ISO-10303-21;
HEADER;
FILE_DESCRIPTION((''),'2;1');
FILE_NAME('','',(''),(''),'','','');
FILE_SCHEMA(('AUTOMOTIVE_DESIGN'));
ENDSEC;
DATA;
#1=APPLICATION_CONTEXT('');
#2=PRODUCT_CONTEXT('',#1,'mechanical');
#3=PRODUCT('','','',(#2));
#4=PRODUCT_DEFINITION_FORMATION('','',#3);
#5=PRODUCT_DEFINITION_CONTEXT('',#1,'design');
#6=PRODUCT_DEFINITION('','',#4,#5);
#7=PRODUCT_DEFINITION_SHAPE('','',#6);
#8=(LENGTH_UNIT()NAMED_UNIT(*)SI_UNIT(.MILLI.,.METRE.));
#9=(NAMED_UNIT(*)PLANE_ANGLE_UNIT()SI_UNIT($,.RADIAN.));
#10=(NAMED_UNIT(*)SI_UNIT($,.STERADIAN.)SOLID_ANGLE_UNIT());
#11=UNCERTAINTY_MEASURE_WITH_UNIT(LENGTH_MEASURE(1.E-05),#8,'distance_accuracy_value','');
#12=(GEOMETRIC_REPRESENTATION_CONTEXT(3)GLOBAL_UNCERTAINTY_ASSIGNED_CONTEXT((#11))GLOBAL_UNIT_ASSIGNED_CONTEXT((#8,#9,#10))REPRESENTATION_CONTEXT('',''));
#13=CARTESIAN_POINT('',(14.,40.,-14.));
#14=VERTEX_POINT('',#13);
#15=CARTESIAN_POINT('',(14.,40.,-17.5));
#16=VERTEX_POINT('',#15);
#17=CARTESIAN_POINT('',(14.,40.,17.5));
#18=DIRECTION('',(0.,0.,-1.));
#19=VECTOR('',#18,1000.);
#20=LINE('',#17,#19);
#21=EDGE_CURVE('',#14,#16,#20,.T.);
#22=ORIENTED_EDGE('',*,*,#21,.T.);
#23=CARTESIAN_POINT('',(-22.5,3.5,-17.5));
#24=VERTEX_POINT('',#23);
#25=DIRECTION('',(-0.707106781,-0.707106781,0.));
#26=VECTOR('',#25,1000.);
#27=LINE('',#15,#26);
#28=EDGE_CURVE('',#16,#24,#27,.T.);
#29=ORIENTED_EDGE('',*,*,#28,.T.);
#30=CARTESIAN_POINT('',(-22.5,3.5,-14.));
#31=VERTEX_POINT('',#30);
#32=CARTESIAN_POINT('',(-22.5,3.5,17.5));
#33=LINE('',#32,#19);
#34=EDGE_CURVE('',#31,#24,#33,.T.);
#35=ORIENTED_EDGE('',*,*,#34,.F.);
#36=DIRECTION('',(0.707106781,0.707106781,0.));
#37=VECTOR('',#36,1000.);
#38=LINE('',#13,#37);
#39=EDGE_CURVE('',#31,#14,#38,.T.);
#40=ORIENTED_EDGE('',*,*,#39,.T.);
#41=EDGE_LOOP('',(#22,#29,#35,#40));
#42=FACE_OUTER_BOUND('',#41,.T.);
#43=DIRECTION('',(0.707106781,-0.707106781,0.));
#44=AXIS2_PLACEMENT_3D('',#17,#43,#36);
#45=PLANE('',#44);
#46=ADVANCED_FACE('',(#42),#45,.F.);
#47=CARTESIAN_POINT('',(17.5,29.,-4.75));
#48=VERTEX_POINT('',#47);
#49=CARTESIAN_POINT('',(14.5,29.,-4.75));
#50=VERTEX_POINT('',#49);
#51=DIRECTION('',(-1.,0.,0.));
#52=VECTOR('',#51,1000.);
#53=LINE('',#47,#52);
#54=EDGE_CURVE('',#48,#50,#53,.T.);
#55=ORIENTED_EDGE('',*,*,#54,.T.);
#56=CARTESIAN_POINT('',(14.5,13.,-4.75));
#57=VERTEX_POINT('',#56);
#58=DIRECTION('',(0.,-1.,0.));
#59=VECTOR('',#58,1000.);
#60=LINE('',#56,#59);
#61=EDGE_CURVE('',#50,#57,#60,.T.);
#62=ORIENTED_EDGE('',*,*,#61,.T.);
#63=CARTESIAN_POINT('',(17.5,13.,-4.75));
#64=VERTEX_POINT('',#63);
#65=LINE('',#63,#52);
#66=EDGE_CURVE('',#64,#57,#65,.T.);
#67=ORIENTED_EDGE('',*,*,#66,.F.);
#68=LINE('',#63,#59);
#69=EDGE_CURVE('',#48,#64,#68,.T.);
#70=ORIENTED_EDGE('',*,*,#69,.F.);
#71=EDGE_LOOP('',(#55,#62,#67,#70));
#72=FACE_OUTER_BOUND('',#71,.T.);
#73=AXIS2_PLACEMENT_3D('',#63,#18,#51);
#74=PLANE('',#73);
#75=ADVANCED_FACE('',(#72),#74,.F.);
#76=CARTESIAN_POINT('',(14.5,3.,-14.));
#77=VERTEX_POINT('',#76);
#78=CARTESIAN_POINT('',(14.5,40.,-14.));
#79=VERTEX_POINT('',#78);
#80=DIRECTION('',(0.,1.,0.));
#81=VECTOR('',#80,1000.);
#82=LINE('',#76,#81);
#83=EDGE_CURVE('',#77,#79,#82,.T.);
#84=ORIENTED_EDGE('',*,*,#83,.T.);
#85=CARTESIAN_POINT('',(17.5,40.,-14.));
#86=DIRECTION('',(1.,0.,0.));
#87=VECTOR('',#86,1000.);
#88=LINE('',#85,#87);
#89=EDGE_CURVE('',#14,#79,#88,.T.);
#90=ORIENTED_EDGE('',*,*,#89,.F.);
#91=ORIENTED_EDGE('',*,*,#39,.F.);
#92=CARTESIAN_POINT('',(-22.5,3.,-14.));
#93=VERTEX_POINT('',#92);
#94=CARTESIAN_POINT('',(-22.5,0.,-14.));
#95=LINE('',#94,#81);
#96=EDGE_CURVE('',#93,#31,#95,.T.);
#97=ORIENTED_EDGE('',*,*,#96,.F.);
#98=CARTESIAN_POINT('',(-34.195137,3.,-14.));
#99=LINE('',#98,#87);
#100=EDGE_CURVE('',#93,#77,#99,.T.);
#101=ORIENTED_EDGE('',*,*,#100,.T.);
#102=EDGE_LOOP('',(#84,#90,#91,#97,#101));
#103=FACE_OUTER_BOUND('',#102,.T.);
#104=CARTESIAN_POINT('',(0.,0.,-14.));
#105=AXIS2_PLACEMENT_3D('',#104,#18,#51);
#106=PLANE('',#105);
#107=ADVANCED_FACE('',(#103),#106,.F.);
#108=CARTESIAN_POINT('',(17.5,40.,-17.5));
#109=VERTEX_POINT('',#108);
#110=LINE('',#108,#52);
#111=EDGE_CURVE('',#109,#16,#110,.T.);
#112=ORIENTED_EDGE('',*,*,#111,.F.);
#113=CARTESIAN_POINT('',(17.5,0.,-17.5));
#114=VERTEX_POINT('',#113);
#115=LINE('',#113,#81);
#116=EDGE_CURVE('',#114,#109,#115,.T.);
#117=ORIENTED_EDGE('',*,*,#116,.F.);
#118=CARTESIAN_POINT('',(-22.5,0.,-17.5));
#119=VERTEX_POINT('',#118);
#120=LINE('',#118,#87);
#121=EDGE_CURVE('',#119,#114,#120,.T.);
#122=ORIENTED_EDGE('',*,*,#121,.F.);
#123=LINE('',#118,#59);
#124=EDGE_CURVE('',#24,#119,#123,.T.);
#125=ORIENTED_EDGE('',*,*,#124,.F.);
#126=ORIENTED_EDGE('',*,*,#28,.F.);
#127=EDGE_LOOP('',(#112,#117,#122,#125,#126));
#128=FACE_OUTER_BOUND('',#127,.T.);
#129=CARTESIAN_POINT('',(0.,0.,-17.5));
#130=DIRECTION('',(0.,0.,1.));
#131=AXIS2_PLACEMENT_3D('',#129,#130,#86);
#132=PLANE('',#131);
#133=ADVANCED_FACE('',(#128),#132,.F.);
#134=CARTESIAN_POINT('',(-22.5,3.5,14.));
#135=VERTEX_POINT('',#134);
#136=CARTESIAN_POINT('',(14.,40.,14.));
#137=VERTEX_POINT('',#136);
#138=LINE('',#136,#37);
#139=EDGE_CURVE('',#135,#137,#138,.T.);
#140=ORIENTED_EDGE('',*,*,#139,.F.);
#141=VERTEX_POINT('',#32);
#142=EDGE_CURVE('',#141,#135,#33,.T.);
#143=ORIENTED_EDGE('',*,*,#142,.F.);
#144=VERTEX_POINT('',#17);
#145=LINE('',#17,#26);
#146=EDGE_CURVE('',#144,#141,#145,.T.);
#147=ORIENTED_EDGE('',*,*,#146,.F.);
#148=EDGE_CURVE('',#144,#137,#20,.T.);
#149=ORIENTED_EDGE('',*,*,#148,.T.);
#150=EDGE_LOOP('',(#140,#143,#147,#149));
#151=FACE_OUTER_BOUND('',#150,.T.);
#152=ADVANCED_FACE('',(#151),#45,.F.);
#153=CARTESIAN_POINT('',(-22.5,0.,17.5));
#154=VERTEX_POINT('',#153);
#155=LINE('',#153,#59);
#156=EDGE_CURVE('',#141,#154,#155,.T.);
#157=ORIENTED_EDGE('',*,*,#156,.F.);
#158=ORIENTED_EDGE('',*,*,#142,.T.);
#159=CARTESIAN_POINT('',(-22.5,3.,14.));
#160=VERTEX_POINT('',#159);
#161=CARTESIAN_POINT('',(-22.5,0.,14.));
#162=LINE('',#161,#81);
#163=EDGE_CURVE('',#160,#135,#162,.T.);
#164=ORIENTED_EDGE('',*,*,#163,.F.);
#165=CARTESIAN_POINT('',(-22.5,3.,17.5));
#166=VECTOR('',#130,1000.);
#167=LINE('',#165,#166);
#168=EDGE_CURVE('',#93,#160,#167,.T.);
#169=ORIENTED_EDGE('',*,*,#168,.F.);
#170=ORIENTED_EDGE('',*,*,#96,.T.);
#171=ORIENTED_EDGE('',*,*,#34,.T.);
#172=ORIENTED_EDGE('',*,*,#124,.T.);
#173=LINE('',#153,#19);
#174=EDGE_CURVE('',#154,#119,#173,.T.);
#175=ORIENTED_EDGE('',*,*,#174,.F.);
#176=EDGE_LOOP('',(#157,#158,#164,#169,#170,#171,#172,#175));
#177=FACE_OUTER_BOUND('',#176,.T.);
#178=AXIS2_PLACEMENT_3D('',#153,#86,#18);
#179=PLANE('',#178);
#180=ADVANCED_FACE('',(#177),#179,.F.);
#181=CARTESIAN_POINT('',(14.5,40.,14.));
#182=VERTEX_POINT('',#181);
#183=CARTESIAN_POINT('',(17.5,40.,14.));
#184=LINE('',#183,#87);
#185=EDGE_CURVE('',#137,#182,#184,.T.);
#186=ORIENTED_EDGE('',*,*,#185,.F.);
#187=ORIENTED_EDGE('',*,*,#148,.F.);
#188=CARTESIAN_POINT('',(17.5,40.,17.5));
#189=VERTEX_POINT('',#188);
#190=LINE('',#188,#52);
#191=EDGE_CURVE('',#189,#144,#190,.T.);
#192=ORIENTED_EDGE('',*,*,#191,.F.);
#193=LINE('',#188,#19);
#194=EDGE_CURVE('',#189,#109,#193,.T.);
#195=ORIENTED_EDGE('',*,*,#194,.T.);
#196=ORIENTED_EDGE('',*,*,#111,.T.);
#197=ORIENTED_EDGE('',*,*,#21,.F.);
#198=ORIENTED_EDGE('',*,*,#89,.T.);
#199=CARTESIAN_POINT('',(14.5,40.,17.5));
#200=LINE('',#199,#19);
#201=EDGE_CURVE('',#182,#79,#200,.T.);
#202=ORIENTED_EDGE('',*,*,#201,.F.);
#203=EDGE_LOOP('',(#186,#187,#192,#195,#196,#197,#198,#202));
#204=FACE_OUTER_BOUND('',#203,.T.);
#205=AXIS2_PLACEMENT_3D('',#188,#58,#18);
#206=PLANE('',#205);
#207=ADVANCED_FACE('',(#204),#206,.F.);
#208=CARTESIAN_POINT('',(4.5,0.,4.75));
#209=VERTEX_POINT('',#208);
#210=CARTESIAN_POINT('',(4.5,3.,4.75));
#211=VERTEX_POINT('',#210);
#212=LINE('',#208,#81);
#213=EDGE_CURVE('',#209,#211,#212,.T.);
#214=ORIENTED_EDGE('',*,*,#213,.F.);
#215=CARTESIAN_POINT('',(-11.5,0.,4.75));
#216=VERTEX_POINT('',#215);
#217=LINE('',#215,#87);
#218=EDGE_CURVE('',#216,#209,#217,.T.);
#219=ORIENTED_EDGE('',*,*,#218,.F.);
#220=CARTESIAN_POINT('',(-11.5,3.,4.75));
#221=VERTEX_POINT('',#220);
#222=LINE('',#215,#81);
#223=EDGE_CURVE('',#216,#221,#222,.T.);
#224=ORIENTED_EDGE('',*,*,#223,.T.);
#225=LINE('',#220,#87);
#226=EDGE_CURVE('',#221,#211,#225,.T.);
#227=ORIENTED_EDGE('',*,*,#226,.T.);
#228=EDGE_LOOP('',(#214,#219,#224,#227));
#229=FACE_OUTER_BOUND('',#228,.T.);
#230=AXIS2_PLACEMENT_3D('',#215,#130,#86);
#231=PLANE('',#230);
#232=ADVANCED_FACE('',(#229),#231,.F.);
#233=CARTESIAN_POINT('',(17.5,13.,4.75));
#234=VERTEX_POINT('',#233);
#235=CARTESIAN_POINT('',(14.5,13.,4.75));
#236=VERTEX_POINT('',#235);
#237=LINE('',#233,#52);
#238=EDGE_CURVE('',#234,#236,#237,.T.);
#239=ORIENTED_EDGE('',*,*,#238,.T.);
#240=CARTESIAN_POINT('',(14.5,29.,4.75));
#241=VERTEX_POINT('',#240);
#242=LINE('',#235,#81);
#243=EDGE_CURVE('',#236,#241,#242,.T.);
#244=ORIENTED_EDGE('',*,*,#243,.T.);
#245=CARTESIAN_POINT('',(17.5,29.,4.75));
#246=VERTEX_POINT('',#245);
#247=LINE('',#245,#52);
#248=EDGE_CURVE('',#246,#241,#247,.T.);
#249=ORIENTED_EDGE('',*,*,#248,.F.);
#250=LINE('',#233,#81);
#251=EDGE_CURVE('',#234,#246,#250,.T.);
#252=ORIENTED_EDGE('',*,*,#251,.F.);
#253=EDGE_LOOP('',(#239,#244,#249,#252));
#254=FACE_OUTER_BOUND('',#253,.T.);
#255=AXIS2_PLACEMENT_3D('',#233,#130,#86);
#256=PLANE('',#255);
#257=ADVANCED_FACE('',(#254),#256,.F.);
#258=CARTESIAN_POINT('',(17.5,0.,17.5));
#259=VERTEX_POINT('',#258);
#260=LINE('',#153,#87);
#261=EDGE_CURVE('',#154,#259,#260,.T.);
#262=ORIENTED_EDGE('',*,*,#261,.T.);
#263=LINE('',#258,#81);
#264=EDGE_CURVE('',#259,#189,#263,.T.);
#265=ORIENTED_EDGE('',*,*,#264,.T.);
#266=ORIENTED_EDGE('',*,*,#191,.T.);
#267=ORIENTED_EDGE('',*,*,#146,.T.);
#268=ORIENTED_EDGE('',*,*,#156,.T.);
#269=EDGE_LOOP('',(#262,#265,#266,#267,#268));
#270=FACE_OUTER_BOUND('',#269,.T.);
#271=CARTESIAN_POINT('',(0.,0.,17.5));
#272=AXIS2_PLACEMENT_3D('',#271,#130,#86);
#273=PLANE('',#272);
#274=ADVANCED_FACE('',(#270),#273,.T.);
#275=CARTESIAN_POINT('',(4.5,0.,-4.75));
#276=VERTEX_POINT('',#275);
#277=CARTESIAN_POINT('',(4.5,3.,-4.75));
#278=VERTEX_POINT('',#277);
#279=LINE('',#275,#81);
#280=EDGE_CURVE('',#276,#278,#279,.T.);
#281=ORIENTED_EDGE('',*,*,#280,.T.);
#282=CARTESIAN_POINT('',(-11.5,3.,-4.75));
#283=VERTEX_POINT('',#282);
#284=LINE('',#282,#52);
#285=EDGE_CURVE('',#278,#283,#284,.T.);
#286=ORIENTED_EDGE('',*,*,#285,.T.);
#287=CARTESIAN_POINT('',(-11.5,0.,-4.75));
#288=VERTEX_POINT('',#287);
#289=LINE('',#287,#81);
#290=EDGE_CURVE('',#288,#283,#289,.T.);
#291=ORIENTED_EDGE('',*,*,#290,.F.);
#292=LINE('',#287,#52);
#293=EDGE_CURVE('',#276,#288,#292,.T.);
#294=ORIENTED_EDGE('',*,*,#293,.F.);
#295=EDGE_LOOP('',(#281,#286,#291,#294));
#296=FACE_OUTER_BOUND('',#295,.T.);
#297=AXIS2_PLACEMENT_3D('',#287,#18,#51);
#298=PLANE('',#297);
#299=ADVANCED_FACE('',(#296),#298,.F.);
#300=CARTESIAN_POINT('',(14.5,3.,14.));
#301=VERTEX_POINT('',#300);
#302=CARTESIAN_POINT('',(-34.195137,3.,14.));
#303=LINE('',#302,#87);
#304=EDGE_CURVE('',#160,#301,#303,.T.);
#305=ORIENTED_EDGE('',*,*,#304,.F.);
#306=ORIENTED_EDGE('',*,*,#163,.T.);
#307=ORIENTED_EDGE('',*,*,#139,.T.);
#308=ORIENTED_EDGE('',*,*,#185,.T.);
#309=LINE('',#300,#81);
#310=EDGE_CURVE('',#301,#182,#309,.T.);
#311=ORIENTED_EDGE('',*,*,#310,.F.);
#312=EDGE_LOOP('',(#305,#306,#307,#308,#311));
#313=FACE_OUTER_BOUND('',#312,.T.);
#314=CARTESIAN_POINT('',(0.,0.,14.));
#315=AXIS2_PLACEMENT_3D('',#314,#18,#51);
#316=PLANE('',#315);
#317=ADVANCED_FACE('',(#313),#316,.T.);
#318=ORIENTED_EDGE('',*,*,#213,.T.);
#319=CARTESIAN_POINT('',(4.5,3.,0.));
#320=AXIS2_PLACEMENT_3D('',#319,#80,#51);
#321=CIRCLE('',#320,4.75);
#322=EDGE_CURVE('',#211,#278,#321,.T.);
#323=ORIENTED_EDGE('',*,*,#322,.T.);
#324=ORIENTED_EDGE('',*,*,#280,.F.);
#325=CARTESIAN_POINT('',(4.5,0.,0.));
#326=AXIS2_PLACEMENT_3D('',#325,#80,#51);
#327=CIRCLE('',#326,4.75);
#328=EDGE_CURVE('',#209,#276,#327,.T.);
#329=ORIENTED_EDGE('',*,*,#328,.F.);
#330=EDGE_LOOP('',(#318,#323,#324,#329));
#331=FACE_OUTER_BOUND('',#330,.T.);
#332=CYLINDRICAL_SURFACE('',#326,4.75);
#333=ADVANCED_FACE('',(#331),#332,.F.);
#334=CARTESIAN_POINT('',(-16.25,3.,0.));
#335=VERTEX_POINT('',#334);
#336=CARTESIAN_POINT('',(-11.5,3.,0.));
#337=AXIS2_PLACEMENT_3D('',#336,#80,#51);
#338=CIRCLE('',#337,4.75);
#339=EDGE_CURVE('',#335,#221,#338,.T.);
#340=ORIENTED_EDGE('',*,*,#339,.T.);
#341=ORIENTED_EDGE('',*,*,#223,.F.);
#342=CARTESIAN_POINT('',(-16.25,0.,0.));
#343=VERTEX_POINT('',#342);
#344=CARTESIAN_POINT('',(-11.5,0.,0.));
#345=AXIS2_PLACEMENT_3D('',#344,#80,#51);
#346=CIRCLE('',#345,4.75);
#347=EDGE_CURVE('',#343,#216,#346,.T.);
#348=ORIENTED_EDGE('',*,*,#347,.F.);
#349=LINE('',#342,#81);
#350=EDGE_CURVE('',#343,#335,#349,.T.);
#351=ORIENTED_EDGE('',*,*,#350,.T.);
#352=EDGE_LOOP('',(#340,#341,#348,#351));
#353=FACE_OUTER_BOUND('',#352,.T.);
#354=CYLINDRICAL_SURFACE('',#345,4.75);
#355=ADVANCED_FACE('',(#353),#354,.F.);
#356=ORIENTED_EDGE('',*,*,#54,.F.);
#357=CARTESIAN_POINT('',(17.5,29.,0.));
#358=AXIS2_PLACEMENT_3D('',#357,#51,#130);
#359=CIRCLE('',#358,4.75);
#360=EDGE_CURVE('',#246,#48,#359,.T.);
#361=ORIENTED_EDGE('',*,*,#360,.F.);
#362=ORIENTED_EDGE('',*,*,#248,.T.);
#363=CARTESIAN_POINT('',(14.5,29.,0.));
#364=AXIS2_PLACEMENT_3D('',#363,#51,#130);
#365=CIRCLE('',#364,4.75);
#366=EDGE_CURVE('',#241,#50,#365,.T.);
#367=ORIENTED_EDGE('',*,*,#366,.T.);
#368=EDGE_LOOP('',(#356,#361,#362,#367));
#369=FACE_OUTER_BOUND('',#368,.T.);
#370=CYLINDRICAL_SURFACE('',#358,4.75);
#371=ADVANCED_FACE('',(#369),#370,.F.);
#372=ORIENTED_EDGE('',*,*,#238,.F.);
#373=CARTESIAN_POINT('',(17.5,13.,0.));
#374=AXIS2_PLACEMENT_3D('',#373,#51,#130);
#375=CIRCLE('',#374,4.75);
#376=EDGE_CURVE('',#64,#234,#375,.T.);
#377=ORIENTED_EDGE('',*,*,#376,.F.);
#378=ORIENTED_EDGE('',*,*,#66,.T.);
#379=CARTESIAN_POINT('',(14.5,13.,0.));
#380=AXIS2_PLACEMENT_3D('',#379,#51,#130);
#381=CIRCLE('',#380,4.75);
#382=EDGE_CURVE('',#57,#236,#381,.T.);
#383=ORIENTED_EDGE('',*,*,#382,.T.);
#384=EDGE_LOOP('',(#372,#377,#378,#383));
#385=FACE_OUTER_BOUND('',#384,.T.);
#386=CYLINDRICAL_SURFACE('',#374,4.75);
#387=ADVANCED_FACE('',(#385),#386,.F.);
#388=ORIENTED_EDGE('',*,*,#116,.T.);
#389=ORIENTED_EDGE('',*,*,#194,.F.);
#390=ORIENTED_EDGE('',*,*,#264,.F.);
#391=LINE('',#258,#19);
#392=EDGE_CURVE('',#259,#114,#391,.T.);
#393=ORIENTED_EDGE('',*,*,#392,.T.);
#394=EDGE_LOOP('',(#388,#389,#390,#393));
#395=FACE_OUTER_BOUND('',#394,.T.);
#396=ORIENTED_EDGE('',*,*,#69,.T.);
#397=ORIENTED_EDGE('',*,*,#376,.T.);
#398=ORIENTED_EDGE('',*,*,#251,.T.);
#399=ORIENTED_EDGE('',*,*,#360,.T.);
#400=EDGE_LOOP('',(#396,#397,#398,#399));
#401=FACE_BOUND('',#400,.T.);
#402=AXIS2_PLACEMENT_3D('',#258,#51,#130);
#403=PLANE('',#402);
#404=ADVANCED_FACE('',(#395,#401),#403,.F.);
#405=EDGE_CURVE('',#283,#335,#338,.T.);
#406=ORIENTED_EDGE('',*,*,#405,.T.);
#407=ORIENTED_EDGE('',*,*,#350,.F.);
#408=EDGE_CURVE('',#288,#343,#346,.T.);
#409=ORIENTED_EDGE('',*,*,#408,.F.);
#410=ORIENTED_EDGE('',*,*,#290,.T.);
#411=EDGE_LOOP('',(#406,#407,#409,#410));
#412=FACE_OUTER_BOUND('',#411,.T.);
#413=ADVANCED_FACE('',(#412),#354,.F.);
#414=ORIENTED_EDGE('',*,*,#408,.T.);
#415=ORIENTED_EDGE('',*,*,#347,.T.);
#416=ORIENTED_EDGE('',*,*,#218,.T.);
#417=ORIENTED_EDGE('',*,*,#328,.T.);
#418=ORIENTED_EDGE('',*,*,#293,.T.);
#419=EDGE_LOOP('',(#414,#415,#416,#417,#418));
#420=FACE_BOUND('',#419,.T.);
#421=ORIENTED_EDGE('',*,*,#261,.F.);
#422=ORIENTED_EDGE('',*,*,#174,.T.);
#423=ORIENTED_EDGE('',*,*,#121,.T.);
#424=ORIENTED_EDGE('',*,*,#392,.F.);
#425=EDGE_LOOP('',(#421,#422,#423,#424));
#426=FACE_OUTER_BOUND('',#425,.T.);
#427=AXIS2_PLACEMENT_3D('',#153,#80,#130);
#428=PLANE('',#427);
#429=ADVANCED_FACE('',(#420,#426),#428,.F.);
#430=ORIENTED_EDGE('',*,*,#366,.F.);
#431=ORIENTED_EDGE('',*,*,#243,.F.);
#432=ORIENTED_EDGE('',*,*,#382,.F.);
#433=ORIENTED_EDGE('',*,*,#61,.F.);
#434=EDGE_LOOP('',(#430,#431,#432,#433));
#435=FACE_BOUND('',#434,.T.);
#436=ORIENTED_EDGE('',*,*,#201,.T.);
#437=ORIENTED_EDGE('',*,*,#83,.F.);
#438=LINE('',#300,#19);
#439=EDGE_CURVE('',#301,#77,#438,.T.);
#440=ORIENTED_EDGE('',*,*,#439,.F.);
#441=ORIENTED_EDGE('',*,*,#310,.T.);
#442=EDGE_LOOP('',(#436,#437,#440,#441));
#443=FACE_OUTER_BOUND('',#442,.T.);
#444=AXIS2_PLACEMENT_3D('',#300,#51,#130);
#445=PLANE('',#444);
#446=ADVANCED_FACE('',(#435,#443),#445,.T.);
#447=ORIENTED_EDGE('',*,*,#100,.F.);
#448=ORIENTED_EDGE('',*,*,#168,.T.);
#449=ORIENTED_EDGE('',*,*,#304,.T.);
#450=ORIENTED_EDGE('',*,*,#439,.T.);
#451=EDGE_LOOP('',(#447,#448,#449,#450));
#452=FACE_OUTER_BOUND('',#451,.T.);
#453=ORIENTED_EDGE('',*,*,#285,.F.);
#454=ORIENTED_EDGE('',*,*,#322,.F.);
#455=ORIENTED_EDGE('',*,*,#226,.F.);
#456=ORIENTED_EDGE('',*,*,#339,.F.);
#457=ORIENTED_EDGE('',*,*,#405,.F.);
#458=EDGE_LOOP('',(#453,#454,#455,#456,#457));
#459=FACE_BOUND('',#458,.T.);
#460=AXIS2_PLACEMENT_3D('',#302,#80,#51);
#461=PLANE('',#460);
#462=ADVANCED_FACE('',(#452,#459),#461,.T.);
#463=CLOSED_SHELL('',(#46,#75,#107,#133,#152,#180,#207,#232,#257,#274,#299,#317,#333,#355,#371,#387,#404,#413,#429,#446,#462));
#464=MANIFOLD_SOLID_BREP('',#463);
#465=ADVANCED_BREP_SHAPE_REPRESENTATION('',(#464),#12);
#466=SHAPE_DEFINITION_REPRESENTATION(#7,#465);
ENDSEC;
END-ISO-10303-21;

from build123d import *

# Parameters (mm, degrees)
EXTRUDE_1_DEPTH     = 17.5
CUT_EXTRUDE_1_DEPTH = 14
CUT_EXTRUDE_2_DEPTH = 47.706530593
CUT_EXTRUDE_3_DEPTH = 58.22979993


with BuildPart() as part:
    # 草图1 → 凸台-拉伸1 (new, symmetric)
    with BuildSketch(Plane.XY):
        Polygon((-22.5, 0), (-22.5, 3.5), (14, 40), (17.5, 40), (17.5, 0), align=None)
    extrude(amount=EXTRUDE_1_DEPTH, both=True)

    # 草图2 → 切除-拉伸1 (cut, symmetric)
    with BuildSketch(Plane.XY):
        Polygon((14.5, 3), (14.5, 49.29015486), (-34.195136802, 3), align=None)
    extrude(amount=CUT_EXTRUDE_1_DEPTH, both=True, mode=Mode.SUBTRACT)

    # 草图4 → 切除-拉伸2 (cut, through all)
    with BuildSketch(Plane(origin=(0, 3, 0), x_dir=(1, 0, 0), z_dir=(0, 1, 0))):
        with BuildLine():
            Line((-11.5, 4.75), (4.5, 4.75))
            ThreePointArc((4.5, 4.75), (9.25, 0), (4.5, -4.75))
            Line((4.5, -4.75), (-11.5, -4.75))
            ThreePointArc((-11.5, -4.75), (-16.25, 0), (-11.5, 4.75))
        make_face()
    extrude(amount=-CUT_EXTRUDE_2_DEPTH, mode=Mode.SUBTRACT)

    # 草图5 → 切除-拉伸3 (cut, through all)
    with BuildSketch(Plane.ZY.offset(-14.5)):
        with BuildLine():
            Line((-4.75, 13), (-4.75, 29))
            ThreePointArc((-4.75, 29), (0, 33.75), (4.75, 29))
            Line((4.75, 29), (4.75, 13))
            ThreePointArc((4.75, 13), (0, 8.25), (-4.75, 13))
        make_face()
    extrude(amount=-CUT_EXTRUDE_3_DEPTH, mode=Mode.SUBTRACT)


solid = part.part
